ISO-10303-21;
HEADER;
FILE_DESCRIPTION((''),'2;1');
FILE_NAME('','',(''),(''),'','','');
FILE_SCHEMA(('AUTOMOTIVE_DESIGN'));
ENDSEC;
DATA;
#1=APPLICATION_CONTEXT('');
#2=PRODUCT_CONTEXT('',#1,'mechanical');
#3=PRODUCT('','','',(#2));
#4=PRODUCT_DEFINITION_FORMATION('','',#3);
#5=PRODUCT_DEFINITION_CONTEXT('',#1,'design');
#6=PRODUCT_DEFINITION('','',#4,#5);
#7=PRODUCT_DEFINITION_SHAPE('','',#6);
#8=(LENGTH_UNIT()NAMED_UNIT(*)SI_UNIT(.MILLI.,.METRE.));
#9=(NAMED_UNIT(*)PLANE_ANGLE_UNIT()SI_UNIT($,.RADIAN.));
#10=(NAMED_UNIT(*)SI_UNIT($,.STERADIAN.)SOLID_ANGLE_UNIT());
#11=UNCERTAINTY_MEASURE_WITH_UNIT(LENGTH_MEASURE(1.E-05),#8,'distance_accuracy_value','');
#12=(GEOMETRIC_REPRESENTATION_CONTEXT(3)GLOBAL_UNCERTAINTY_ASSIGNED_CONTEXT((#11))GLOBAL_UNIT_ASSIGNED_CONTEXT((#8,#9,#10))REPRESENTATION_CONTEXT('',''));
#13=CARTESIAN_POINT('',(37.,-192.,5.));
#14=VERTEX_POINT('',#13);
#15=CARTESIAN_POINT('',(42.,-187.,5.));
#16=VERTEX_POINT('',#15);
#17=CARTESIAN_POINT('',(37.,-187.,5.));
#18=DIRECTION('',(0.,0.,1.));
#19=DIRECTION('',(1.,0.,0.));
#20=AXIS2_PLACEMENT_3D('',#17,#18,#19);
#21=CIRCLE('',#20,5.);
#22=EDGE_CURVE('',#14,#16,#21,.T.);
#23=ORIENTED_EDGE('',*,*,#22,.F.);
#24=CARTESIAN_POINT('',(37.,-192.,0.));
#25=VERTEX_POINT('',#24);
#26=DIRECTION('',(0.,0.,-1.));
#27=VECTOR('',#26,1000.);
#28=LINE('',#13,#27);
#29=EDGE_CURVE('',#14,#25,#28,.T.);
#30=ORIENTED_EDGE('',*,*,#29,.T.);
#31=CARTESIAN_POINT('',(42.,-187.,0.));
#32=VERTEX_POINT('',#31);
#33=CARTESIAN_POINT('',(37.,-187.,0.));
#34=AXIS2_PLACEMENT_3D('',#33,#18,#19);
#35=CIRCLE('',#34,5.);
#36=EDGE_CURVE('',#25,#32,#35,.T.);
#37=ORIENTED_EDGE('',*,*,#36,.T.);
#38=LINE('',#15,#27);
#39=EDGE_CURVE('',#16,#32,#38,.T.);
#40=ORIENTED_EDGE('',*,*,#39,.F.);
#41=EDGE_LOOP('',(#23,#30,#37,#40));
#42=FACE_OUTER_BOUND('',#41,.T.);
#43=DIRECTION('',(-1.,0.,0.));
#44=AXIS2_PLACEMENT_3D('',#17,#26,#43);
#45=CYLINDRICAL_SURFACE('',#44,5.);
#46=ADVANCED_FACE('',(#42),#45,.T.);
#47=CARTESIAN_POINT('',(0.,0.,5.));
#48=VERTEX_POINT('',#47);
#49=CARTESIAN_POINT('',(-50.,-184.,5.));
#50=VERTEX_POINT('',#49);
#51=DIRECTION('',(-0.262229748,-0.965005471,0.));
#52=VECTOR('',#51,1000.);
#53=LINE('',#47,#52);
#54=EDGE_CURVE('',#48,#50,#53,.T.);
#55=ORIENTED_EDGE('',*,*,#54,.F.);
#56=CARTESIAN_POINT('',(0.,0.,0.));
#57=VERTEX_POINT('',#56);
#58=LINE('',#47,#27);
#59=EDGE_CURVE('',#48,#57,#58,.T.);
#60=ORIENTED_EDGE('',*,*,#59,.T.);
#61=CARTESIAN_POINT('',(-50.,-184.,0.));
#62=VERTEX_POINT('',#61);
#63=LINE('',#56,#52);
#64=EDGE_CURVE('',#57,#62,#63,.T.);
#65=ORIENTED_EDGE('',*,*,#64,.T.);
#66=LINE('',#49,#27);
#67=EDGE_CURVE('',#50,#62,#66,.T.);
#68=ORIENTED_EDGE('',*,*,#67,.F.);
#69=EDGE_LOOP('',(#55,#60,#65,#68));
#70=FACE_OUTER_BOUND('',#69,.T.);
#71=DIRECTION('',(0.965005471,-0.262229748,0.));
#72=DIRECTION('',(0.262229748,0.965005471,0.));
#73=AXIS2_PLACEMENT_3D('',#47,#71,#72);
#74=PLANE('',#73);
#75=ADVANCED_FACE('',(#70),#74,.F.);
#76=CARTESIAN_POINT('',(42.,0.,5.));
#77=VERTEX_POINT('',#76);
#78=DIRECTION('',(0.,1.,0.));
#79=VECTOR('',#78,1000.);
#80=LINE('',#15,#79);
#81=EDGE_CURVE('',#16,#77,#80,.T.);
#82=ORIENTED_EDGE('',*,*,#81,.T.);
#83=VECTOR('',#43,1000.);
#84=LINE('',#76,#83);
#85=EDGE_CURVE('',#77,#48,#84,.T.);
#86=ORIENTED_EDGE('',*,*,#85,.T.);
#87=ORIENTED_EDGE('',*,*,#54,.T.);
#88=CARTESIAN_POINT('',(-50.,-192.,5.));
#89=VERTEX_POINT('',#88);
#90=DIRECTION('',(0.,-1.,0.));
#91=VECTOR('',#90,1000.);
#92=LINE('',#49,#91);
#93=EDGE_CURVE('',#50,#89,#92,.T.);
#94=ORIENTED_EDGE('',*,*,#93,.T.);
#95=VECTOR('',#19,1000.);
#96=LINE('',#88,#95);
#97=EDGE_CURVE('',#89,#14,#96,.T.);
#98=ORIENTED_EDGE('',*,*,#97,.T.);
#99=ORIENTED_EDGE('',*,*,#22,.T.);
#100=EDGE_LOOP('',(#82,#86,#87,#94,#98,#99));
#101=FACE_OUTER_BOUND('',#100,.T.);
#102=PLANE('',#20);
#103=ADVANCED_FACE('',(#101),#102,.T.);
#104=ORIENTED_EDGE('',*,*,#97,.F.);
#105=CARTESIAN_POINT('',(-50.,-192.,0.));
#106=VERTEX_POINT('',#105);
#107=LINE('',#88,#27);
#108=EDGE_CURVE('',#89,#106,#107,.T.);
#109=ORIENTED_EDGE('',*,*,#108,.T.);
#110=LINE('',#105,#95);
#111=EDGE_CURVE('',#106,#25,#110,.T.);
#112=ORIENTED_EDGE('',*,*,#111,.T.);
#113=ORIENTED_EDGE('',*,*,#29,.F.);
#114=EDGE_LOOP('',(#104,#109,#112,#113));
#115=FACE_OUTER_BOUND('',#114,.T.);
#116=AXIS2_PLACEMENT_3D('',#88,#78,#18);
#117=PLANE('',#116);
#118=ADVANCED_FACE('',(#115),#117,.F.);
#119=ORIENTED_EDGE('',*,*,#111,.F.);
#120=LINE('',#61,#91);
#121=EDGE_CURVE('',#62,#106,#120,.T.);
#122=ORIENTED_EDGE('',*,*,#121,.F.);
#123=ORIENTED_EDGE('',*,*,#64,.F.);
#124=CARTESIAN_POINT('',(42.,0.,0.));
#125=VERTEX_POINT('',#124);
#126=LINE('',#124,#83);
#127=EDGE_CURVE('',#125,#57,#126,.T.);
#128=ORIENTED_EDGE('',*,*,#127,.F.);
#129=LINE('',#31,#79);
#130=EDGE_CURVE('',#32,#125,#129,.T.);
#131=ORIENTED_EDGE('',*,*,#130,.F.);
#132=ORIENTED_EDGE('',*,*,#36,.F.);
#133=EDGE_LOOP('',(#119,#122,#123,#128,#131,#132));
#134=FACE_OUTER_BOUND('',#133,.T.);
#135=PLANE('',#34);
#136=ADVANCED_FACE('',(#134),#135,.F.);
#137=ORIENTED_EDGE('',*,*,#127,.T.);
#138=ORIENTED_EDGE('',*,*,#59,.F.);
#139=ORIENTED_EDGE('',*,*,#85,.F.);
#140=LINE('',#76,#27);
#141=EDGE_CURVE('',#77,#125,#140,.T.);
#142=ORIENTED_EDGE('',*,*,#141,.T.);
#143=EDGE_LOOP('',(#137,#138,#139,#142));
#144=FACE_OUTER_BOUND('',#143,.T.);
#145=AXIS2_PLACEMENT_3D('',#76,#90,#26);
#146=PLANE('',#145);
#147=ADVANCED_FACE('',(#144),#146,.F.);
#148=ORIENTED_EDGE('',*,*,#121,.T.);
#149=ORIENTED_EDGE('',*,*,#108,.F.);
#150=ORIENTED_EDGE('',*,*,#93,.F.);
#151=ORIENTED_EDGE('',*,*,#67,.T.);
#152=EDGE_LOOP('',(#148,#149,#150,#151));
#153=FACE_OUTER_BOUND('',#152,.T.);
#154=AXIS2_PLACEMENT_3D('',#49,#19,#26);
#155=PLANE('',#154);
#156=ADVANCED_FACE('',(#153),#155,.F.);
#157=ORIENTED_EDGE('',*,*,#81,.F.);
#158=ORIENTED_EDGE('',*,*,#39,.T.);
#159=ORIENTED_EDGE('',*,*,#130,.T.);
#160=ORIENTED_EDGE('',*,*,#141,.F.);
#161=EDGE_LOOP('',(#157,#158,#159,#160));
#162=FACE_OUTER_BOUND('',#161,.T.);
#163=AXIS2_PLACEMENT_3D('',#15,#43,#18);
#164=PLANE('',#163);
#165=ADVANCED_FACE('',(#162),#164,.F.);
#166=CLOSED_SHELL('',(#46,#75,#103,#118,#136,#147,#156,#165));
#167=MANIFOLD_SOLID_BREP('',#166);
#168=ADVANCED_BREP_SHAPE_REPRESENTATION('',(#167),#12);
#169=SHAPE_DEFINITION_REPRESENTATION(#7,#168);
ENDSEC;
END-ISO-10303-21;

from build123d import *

# Parameters (mm, degrees)
BOSS_EXTRUDE1_DEPTH = 5


with BuildPart() as part:
    # Sketch1 → Boss-Extrude1 (new body)
    with BuildSketch(Plane.XY):
        with BuildLine():
            Line((0, 0), (-50, -184))
            Line((-50, -184), (-50, -192))
            Line((-50, -192), (37, -192))
            ThreePointArc((37, -192), (40.535533906, -190.535533906), (42, -187))
            Line((42, -187), (42, 0))
            Line((42, 0), (0, 0))
        make_face()
    extrude(amount=BOSS_EXTRUDE1_DEPTH)


solid = part.part
